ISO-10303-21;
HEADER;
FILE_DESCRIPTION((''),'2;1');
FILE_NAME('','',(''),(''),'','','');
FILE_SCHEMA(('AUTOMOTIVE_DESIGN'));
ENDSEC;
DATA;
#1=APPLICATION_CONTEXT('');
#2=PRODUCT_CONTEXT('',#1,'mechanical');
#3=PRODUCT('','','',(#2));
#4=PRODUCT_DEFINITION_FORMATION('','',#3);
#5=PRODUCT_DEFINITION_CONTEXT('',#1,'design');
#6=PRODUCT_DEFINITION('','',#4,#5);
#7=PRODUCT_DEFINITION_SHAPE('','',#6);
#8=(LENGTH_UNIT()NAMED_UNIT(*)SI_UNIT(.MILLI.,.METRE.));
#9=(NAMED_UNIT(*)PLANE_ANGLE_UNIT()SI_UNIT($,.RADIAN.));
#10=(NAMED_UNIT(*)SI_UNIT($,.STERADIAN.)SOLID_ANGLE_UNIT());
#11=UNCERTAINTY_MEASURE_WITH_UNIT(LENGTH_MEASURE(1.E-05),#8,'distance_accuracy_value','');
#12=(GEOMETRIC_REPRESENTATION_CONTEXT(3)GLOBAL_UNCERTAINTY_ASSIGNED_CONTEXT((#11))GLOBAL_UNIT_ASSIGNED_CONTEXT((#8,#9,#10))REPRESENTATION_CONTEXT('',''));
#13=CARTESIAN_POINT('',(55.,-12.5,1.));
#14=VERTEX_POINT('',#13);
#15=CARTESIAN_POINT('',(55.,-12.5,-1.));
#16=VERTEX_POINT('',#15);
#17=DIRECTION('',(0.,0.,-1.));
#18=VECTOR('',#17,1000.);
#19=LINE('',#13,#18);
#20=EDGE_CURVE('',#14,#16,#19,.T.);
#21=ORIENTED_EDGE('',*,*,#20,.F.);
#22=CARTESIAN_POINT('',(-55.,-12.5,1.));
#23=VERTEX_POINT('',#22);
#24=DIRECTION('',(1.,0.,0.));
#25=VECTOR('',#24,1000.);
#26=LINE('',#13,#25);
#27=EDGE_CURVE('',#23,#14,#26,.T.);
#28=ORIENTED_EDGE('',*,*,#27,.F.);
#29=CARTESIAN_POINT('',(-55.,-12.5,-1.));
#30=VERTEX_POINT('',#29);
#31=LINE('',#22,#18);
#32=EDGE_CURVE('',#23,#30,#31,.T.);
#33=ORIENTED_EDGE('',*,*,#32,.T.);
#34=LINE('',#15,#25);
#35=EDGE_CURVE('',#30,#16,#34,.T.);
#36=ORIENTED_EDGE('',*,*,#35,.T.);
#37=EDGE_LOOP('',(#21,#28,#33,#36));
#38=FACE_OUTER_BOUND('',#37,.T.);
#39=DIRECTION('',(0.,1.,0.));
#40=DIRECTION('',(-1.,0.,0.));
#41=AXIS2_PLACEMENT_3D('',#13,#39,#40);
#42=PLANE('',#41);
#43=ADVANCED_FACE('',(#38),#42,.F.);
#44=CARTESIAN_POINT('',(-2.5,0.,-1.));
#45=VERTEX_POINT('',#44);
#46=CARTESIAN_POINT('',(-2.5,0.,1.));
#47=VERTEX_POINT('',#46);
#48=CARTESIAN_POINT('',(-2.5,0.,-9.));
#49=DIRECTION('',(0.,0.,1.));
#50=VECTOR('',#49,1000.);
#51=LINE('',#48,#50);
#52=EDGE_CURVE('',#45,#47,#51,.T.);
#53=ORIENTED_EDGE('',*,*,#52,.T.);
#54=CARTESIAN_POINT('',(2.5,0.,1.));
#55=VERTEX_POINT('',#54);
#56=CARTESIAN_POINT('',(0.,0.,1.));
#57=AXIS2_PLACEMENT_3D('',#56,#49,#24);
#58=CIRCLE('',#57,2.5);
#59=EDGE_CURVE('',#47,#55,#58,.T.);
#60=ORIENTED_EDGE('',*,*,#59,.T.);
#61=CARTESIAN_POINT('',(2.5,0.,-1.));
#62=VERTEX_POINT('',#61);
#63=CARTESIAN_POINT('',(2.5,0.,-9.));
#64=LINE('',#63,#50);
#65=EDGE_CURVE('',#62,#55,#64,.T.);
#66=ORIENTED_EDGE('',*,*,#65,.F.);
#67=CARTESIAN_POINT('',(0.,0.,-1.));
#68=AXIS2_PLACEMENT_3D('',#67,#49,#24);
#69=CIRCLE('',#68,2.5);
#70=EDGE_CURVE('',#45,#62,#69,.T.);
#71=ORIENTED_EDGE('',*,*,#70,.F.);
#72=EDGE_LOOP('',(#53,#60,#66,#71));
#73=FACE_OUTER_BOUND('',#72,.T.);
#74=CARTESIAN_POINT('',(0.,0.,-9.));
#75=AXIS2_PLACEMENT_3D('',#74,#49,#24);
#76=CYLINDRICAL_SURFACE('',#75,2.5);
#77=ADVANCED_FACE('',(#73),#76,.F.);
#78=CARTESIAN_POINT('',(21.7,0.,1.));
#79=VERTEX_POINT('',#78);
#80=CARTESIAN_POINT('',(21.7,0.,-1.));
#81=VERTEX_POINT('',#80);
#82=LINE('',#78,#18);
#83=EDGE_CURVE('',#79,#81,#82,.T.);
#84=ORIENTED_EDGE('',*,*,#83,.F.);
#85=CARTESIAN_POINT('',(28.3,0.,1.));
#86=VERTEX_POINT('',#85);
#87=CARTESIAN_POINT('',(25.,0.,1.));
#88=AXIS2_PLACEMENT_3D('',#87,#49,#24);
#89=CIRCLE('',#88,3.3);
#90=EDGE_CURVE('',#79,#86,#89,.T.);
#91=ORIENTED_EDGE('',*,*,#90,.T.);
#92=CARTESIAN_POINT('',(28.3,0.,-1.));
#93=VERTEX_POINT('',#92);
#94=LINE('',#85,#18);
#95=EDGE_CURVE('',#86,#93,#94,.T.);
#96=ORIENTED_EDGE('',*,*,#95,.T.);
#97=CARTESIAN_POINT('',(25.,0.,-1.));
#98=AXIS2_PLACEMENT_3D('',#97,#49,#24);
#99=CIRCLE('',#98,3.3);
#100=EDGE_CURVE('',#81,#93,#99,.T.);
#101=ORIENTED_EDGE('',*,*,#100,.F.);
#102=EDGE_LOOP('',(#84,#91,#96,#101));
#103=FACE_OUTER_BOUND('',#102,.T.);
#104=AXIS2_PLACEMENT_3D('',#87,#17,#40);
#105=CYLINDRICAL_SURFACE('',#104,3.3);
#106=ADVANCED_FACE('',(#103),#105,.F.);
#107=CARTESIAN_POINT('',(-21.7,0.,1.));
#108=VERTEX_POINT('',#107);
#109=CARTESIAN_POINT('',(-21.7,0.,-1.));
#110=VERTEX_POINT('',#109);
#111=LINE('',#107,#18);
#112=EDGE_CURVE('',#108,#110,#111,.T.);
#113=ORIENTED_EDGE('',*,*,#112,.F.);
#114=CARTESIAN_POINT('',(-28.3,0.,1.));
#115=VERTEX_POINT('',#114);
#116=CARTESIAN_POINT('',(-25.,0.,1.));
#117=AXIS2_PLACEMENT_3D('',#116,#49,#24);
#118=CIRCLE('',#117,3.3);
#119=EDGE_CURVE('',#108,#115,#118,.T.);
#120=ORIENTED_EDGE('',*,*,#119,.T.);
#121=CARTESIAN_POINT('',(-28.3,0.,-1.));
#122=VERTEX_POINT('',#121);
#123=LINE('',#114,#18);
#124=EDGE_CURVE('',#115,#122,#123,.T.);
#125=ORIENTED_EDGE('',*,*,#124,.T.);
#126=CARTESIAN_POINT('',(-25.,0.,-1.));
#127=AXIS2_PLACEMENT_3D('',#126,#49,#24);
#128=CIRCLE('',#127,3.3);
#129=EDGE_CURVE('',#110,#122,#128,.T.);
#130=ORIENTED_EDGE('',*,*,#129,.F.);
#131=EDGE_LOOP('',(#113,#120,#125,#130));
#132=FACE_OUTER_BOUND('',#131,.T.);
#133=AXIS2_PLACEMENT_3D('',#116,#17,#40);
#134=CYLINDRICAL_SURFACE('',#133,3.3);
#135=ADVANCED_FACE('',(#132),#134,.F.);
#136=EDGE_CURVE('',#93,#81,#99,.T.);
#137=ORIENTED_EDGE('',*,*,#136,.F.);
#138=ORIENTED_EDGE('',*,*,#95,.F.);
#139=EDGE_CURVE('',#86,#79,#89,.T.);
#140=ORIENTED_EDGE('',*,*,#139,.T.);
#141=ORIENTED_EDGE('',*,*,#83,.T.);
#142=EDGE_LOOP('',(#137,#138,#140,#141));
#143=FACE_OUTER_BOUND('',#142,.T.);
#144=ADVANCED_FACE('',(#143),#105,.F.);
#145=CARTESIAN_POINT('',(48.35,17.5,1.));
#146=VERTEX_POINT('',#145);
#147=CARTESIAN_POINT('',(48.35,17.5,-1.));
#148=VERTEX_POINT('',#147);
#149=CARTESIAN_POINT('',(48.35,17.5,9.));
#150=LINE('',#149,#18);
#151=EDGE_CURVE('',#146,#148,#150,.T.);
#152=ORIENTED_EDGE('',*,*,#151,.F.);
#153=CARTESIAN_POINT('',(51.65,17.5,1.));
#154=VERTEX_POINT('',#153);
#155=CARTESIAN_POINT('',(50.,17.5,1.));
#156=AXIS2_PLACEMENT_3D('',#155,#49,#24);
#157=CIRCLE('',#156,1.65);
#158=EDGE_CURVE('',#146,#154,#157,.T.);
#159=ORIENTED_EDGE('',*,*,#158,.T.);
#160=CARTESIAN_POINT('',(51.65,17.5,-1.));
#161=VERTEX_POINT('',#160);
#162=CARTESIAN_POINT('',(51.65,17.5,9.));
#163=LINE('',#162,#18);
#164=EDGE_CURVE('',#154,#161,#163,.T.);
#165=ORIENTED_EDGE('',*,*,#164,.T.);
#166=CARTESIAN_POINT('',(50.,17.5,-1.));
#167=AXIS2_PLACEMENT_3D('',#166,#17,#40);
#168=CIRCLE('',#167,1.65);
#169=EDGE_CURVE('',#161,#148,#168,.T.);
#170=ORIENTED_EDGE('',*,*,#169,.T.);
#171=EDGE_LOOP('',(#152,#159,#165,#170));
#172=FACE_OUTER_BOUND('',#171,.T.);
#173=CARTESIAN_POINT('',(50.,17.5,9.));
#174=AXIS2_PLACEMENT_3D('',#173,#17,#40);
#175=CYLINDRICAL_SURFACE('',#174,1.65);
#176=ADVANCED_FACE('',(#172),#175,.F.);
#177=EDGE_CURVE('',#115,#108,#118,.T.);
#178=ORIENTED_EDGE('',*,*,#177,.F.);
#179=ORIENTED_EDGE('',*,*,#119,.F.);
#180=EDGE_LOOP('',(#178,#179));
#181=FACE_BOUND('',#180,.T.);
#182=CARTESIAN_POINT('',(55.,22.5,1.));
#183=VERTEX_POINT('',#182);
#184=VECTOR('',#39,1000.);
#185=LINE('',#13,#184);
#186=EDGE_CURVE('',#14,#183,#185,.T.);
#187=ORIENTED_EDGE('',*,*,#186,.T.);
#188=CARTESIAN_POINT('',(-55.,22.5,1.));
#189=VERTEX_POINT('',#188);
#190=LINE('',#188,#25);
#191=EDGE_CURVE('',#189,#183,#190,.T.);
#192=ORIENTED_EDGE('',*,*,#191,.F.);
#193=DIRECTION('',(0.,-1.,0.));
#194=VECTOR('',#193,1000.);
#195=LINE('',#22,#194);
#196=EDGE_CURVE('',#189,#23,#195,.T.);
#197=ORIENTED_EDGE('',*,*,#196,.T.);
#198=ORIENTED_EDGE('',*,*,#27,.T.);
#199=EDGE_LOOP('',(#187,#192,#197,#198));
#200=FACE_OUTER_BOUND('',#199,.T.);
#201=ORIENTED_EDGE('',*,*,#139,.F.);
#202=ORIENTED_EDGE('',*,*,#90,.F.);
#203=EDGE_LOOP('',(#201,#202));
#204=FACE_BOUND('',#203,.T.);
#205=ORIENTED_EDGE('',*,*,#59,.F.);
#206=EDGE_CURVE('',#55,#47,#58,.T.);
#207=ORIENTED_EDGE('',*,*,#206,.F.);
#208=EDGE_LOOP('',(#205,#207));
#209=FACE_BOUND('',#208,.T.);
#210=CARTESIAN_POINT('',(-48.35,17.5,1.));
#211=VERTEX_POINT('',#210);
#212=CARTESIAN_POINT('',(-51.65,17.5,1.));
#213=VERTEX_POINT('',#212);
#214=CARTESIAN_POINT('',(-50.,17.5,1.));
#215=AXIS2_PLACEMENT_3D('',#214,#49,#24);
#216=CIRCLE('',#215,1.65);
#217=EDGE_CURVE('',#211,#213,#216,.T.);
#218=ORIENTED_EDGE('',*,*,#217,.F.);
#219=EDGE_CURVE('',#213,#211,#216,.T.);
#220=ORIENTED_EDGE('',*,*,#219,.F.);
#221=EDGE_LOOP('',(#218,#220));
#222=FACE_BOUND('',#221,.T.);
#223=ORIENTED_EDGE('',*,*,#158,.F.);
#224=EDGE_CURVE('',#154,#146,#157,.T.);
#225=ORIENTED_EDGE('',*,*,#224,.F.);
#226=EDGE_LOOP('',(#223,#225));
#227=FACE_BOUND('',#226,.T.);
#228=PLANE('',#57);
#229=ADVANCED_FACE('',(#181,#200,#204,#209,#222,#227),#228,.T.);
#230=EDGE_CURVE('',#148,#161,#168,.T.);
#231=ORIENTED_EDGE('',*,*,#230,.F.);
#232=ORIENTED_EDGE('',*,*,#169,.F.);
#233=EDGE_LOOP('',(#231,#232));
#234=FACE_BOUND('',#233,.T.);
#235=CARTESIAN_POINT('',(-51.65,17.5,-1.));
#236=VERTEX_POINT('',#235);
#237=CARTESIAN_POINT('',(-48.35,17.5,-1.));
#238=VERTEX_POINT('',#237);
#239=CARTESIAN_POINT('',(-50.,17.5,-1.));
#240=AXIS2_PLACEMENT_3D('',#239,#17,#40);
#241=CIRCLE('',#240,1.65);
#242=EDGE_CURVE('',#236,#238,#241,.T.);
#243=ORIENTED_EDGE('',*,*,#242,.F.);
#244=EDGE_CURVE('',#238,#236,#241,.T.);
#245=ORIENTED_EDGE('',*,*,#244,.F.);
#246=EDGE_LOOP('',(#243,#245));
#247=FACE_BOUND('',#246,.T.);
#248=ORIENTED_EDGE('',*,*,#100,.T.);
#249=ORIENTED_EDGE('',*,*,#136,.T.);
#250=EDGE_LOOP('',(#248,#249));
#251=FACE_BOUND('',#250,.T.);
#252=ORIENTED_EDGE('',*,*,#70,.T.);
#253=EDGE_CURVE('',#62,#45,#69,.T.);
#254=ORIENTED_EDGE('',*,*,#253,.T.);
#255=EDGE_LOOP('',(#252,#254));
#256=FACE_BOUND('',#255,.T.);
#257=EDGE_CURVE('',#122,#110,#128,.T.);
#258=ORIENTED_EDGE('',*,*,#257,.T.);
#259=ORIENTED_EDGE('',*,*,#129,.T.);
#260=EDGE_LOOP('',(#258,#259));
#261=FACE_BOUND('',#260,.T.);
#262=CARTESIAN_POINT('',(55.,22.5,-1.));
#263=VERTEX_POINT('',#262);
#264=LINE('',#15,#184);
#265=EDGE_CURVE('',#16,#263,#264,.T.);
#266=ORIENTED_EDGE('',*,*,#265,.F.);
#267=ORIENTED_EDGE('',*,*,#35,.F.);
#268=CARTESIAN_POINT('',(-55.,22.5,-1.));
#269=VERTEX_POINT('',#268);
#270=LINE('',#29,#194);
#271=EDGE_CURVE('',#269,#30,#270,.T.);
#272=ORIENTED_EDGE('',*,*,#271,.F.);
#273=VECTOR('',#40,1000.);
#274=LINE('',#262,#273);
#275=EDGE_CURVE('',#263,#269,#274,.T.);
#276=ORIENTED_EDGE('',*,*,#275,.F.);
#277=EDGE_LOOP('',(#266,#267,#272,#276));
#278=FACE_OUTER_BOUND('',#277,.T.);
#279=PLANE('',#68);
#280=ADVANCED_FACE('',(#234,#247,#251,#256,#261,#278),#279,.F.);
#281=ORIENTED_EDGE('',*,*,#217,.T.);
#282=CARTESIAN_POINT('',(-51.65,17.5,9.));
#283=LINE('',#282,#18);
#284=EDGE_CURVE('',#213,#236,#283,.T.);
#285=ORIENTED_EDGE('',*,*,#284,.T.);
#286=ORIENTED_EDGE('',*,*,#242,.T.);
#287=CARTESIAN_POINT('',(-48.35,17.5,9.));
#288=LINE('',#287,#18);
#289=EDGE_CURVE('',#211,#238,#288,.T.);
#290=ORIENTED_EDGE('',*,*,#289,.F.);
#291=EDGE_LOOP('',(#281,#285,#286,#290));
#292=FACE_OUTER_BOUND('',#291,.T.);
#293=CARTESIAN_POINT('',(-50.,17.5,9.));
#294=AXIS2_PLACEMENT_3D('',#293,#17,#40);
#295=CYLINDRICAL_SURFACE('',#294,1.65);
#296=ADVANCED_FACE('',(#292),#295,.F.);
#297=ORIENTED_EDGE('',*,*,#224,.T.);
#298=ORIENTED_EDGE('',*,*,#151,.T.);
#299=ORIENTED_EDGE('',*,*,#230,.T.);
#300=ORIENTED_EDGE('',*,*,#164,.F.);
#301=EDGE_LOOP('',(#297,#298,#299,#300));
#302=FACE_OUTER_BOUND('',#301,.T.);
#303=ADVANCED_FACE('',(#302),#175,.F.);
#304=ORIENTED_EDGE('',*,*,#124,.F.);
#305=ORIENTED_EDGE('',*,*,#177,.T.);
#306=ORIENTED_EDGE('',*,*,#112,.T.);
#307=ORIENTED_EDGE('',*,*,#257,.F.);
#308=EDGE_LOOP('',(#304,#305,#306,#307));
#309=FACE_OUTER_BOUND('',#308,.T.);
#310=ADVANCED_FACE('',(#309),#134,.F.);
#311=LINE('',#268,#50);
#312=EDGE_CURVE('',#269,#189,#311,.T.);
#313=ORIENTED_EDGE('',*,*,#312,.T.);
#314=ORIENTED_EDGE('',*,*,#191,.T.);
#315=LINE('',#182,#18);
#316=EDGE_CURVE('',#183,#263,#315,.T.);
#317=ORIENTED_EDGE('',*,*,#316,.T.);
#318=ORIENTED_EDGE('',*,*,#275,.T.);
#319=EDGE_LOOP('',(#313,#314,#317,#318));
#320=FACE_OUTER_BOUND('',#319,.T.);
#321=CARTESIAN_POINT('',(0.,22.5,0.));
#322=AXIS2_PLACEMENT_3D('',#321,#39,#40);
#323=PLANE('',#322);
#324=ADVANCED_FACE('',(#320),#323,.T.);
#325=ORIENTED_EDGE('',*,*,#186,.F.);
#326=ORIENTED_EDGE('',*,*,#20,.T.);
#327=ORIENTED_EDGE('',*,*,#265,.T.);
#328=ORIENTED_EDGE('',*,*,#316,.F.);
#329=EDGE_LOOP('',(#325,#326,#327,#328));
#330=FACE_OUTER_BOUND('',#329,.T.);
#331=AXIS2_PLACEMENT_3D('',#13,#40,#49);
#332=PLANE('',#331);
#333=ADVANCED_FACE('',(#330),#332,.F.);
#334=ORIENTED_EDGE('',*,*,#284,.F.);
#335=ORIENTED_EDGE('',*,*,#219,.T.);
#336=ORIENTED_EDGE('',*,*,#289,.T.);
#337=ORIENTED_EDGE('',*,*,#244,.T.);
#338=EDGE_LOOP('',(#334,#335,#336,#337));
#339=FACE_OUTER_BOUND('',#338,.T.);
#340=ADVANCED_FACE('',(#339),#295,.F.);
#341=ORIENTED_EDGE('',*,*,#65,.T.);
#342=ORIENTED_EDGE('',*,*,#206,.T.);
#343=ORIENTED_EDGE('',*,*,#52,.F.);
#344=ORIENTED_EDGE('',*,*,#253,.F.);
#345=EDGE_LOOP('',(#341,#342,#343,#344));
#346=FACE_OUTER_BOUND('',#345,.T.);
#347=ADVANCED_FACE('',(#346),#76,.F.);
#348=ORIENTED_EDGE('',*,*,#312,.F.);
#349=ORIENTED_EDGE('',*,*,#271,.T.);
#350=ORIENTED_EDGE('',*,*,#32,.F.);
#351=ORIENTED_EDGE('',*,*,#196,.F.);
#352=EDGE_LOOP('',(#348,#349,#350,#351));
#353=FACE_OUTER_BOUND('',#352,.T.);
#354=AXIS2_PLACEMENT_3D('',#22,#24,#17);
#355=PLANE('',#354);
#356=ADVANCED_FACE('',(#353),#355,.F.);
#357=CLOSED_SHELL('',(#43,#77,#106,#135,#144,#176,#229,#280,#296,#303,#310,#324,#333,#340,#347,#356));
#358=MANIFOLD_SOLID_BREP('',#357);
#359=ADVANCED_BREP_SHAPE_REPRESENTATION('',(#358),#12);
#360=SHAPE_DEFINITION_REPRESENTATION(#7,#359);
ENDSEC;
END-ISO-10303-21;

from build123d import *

# Parameters (mm, degrees)
SKETCH_1_W          = 110
SKETCH_1_H          = 25
SKETCH_1_R          = 3.3
EXTRUDE_1_DEPTH     = 1
SKETCH_2_R          = 2.5
CUT_EXTRUDE_1_DEPTH = 10
SKETCH_3_W          = 110
SKETCH_3_H          = 2
EXTRUDE_2_DEPTH     = 10
SKETCH_4_R          = 1.65
CUT_EXTRUDE_2_DEPTH = 10


with BuildPart() as part:
    # 草图1 → 凸台-拉伸1 (new, symmetric)
    with BuildSketch(Plane.XY):
        Rectangle(SKETCH_1_W, SKETCH_1_H)
        with Locations((-25, 0)):
            Circle(SKETCH_1_R, mode=Mode.SUBTRACT)
        with Locations((25, 0)):
            Circle(SKETCH_1_R, mode=Mode.SUBTRACT)
    extrude(amount=EXTRUDE_1_DEPTH, both=True)

    # 草图2 → 切除-拉伸1 (cut)
    with BuildSketch(Plane.XY.offset(1)):
        Circle(SKETCH_2_R)
    extrude(amount=-CUT_EXTRUDE_1_DEPTH, mode=Mode.SUBTRACT)

    # 草图3 → 凸台-拉伸2 (add)
    with BuildSketch(Plane(origin=(0, 12.5, 0), x_dir=(1, 0, 0), z_dir=(0, 1, 0))):
        Rectangle(SKETCH_3_W, SKETCH_3_H)
    extrude(amount=EXTRUDE_2_DEPTH)

    # 草图4 → 切除-拉伸2 (cut)
    with BuildSketch(Plane(origin=(0, 0, -1), x_dir=(-1, 0, 0), z_dir=(0, 0, -1))):
        with Locations((-50, 17.5)):
            Circle(SKETCH_4_R)
        with Locations((50, 17.5)):
            Circle(SKETCH_4_R)
    extrude(amount=-CUT_EXTRUDE_2_DEPTH, mode=Mode.SUBTRACT)


solid = part.part
